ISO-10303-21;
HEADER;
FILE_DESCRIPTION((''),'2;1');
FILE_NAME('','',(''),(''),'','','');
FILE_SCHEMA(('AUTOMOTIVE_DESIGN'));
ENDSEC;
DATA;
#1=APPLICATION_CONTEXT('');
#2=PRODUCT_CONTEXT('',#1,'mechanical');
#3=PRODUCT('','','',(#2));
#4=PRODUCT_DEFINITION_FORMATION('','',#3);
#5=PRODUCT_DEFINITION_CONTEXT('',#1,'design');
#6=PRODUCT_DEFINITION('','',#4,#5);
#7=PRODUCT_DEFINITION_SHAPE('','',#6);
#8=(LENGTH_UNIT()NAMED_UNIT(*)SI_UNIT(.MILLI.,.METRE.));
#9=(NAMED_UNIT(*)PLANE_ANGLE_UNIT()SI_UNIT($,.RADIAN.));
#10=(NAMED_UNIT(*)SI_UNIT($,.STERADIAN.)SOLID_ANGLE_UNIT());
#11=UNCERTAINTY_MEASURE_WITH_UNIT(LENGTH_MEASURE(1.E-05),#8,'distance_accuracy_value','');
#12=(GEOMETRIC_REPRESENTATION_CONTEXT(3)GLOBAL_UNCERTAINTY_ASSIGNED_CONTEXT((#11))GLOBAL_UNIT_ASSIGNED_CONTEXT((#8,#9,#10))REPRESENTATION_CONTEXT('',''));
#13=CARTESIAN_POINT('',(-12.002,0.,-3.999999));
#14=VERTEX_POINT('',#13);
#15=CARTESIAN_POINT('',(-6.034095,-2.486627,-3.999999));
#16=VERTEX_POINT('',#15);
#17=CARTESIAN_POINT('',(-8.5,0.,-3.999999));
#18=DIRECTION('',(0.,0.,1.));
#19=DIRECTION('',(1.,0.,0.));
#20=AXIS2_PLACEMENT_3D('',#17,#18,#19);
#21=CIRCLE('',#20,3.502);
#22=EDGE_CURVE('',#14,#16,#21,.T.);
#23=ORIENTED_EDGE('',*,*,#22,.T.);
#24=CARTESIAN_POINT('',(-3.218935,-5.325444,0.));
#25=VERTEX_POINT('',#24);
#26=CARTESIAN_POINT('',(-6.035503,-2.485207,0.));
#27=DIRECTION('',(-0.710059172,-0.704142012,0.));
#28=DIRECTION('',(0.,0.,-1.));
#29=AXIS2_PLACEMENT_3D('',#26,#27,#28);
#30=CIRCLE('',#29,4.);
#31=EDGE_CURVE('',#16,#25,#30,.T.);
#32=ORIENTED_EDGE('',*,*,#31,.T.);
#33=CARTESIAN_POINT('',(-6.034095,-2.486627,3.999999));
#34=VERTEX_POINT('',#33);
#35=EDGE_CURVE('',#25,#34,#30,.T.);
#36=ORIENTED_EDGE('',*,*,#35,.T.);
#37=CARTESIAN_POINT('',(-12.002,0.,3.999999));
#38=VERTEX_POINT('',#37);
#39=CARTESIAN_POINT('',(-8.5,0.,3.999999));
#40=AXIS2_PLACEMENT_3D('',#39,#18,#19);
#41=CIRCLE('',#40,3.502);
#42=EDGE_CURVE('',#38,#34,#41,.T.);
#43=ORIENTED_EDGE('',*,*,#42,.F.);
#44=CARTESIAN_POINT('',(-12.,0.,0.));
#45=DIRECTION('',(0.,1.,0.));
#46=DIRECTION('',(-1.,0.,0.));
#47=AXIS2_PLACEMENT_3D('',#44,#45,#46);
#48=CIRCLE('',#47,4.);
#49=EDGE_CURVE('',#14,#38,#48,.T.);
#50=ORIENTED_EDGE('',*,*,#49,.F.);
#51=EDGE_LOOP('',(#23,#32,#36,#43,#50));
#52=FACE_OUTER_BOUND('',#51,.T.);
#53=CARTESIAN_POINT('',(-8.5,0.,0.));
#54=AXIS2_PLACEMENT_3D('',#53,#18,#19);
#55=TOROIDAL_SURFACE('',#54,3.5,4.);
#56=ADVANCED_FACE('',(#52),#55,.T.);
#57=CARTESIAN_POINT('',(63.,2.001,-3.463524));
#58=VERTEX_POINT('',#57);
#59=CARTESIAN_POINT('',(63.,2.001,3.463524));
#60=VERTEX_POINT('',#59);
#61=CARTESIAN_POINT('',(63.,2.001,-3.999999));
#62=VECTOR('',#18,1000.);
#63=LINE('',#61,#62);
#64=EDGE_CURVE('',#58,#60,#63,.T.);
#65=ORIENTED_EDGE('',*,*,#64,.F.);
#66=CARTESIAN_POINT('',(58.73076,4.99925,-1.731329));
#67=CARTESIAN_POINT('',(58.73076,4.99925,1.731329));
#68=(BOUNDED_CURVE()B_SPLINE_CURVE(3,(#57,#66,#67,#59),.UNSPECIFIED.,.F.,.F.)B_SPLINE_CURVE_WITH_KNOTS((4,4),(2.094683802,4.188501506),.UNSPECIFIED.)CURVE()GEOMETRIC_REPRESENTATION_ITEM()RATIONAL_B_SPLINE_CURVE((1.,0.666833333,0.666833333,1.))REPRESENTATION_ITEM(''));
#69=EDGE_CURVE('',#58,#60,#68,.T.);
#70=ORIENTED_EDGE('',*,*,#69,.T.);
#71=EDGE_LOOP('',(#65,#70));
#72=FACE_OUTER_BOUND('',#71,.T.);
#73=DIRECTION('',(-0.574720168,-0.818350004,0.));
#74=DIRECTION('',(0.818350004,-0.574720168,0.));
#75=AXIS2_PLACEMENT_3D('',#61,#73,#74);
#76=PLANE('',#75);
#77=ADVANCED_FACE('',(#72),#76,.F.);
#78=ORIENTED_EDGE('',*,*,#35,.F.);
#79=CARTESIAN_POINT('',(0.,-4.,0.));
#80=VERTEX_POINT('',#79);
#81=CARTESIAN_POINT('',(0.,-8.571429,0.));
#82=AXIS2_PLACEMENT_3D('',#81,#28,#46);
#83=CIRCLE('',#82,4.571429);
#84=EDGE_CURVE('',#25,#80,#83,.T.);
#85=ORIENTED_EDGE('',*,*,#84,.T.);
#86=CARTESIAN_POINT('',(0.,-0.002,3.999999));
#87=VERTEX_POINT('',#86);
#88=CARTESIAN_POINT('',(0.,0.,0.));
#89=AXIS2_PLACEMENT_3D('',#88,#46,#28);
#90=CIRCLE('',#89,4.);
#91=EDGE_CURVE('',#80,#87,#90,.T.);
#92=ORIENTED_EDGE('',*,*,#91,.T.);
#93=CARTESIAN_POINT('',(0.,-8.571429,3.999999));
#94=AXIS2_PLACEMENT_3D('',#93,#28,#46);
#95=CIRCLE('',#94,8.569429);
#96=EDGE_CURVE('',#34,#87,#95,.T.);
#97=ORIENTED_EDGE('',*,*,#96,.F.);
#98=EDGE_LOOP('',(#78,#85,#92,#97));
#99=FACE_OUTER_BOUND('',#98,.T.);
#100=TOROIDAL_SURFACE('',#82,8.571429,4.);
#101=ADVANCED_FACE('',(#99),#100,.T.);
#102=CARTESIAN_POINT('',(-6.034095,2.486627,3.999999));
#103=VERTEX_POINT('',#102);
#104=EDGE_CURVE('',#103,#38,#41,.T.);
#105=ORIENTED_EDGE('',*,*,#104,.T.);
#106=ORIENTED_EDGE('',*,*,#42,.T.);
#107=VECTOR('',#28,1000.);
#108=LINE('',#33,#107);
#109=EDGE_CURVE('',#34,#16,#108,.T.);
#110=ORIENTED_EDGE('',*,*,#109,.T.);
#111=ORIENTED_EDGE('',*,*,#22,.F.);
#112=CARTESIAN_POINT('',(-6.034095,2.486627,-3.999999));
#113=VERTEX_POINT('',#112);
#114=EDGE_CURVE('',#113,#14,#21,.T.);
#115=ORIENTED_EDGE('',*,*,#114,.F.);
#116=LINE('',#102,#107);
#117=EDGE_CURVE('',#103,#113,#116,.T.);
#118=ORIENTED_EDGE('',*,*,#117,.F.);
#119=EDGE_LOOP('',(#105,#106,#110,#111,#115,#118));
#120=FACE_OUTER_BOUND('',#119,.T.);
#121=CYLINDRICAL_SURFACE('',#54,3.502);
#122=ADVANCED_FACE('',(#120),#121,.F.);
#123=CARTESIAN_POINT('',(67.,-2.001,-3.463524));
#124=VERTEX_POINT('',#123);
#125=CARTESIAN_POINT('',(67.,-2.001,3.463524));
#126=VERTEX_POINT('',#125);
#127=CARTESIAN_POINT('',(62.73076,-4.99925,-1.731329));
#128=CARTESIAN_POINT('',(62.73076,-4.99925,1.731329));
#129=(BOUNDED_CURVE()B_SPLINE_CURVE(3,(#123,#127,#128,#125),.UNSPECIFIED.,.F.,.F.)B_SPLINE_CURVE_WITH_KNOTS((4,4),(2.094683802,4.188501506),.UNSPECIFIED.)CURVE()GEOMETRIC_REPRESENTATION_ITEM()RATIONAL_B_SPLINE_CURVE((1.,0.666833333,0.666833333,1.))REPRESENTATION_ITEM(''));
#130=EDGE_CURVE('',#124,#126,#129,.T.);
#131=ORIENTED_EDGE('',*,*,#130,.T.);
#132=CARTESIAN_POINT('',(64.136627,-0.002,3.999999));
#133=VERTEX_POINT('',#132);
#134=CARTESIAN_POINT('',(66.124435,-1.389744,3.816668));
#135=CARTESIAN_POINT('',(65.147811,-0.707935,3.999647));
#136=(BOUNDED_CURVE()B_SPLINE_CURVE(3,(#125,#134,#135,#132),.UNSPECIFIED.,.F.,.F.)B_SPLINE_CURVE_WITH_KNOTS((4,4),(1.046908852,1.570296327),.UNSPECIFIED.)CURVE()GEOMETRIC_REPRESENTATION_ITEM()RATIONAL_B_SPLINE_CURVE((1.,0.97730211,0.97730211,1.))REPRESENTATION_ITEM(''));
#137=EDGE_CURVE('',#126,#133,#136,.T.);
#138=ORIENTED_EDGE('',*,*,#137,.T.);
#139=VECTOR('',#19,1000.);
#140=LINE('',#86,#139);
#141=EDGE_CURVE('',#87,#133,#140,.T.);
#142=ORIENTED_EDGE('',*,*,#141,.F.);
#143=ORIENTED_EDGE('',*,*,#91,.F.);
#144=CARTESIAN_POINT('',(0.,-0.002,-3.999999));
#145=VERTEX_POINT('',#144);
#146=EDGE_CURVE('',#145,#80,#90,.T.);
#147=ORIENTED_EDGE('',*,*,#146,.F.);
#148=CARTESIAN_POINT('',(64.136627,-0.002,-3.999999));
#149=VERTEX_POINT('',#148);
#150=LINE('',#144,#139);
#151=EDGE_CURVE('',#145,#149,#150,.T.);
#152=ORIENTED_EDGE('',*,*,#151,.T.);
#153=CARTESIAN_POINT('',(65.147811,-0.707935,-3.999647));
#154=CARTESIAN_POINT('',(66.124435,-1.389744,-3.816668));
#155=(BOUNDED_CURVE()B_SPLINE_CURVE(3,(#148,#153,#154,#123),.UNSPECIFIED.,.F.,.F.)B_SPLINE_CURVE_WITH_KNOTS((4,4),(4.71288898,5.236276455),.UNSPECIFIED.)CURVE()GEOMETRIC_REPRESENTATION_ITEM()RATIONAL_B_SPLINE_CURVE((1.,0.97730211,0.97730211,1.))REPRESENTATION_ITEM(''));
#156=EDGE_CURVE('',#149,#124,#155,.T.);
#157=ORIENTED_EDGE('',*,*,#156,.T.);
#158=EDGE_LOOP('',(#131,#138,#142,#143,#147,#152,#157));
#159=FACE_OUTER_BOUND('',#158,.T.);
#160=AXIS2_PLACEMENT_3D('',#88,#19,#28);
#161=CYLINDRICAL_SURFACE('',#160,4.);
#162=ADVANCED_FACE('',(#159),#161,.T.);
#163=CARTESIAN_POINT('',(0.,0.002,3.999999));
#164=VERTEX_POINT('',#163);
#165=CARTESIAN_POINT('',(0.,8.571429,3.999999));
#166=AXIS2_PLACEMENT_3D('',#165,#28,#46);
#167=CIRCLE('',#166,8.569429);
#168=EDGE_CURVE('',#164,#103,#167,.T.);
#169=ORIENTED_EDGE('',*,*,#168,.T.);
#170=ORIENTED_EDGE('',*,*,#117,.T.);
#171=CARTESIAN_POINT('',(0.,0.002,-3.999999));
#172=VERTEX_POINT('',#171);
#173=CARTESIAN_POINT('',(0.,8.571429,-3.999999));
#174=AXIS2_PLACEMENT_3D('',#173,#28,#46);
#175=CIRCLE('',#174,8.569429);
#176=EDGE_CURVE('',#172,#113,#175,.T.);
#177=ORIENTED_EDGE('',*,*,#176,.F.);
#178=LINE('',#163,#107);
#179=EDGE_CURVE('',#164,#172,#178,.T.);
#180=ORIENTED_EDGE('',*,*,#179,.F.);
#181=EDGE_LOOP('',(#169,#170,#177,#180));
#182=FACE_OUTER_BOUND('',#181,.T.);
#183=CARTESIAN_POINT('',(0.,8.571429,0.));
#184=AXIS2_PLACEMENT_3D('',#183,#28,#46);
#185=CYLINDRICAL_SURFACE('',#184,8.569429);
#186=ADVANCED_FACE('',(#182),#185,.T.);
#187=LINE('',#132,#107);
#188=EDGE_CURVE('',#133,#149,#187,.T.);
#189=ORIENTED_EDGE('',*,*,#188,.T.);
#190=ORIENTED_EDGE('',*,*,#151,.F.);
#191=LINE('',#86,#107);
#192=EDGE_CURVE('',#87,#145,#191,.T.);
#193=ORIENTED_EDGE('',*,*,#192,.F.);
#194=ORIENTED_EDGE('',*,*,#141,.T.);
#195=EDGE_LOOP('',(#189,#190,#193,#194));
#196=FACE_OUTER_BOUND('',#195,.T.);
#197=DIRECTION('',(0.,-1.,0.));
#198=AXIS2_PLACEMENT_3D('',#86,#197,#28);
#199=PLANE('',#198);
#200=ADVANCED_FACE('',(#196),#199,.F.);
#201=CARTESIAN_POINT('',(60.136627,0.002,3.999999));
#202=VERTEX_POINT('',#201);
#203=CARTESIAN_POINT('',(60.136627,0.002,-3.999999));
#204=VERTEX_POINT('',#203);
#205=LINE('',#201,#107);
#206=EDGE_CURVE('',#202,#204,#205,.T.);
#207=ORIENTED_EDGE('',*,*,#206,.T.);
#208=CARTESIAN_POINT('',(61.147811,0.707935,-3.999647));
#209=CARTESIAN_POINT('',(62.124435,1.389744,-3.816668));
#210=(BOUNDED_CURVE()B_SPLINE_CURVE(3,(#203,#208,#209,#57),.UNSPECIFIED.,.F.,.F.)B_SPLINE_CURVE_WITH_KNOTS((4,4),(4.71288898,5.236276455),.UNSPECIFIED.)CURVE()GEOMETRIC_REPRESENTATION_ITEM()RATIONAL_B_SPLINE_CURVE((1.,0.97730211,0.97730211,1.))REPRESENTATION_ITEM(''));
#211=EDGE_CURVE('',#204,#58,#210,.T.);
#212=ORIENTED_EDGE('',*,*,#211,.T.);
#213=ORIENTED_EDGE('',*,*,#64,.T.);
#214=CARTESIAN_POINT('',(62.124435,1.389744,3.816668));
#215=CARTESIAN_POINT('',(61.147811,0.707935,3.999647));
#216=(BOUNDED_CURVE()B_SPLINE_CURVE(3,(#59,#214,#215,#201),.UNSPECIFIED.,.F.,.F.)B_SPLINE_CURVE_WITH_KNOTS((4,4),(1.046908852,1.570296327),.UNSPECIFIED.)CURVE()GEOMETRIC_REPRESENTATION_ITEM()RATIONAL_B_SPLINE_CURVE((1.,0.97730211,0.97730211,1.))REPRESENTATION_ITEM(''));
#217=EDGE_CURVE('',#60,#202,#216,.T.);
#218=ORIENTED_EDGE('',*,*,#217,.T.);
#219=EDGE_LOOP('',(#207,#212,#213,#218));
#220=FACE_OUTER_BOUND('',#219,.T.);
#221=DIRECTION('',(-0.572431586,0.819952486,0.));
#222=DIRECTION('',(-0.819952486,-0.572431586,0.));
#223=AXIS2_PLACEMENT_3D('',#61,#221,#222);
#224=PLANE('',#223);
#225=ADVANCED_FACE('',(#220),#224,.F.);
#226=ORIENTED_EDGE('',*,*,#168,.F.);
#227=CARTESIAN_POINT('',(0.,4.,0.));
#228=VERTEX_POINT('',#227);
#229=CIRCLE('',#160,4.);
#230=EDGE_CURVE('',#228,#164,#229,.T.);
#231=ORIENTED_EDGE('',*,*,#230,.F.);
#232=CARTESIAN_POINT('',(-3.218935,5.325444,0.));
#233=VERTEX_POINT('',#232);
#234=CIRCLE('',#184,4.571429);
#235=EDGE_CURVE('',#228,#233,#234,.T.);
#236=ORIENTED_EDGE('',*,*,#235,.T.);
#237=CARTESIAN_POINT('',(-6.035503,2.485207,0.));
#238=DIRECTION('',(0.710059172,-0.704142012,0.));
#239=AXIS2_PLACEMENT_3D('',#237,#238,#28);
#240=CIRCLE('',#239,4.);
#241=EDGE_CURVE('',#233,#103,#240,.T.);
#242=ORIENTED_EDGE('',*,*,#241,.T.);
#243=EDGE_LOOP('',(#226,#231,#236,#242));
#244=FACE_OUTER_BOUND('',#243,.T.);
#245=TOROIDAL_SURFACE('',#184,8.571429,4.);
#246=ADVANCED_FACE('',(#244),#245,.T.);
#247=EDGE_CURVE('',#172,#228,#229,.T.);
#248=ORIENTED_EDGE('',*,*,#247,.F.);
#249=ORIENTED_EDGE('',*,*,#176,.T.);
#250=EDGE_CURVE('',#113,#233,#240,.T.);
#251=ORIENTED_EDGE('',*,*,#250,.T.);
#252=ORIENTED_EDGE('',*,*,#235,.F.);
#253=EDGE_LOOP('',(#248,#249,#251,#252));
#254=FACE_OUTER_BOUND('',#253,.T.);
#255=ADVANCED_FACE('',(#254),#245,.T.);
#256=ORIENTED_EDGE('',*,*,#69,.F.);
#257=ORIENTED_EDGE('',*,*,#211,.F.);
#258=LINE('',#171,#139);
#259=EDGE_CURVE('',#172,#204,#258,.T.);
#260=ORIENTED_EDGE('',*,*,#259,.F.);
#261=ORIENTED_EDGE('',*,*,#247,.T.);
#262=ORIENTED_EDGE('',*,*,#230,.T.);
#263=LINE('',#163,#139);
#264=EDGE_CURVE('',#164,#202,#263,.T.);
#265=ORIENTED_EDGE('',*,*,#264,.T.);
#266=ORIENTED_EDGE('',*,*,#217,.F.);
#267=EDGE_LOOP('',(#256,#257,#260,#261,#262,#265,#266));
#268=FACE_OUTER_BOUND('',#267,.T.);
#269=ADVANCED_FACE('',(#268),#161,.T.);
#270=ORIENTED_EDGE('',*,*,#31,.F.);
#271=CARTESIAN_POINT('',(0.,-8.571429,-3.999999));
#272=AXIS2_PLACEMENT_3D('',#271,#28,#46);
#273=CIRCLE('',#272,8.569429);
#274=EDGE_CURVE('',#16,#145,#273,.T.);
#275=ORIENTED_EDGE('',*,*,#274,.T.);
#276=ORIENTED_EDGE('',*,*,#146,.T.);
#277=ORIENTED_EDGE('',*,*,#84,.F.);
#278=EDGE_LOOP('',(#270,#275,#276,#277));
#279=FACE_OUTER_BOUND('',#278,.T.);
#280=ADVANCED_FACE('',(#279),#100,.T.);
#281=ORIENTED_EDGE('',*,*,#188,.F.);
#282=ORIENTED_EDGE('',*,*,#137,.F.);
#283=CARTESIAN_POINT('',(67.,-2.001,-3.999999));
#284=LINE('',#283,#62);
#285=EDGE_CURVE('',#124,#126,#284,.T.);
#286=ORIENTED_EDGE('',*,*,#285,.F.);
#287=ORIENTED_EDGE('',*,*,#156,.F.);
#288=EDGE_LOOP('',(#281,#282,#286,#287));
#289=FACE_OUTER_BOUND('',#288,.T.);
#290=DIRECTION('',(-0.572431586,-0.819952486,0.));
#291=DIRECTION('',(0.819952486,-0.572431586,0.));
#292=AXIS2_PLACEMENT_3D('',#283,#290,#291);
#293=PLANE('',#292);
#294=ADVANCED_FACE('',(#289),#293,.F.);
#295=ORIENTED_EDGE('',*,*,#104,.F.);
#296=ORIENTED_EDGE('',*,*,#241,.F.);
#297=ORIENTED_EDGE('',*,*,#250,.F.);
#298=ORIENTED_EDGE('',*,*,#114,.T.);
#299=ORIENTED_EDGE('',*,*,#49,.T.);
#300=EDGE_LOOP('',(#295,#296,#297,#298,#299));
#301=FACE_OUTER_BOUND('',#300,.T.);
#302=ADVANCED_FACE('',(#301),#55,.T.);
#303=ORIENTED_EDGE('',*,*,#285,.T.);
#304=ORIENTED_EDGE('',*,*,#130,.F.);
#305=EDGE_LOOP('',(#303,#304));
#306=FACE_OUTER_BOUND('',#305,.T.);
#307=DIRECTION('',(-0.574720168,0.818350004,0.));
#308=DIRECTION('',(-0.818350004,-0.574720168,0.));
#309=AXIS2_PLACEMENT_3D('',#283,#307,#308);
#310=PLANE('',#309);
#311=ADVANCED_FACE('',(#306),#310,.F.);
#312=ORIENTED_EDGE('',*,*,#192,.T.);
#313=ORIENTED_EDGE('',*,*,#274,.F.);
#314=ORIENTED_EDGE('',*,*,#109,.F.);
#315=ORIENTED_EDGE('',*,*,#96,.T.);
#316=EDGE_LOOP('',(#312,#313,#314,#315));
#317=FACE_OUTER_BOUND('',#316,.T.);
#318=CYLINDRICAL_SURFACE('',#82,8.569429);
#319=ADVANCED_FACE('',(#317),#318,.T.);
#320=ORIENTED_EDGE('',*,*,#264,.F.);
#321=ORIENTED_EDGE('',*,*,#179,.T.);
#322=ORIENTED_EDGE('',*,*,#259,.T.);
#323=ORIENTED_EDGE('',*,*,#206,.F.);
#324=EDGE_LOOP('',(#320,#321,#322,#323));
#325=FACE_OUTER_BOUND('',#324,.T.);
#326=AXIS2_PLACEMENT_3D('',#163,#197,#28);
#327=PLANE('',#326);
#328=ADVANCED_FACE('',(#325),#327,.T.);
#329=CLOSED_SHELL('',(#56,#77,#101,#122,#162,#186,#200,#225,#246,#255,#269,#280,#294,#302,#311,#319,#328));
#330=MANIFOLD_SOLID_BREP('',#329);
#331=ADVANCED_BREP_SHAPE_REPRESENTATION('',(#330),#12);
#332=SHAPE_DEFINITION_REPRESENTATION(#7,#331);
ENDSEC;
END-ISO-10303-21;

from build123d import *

# Parameters (mm, degrees)
CONECUT_DEPTH      = 68.537026869
CONECUT_DEPTH_BACK = 68.537026869


with BuildPart() as part:
    # Body: sweep along a path in 草图2
    with BuildLine(Plane.XY) as body_path:
        Line((63, 4), (0, 4))
        ThreePointArc((0, 4), (-1.740570538, 4.344328693), (-3.218934911, 5.325443787))
        ThreePointArc((-3.218934911, 5.325443787), (-16, 0), (-3.218934911, -5.325443787))
        ThreePointArc((-3.218934911, -5.325443787), (-1.740570538, -4.344328693), (0, -4))
        Line((0, -4), (67, -4))
    # 草图1 → Body (sweep)
    with BuildSketch(Plane(origin=(63, 0, 0), x_dir=(0, 0, -1), z_dir=(1, 0, 0))):
        with BuildLine():
            Line((-3.9999995, 0.002), (3.9999995, 0.002))
            ThreePointArc((3.9999995, 0.002), (0, 4), (-3.9999995, 0.002))
        make_face()
    sweep(path=body_path.line)

    # 草图3 → ConeCut (cut, two sides: drawn at the far end of the back side and taken through both)
    with BuildSketch(Plane.XY.offset(-CONECUT_DEPTH_BACK)):
        Polygon((63, 2.001), (60.139364077, 4.01), (67.01, 4.01), (67.01, -4.01), (64.139364077, -4.01), (67, -2.001), (64.133762416, 0), (60.133762416, 0), align=None)
    extrude(amount=CONECUT_DEPTH + CONECUT_DEPTH_BACK, mode=Mode.SUBTRACT)


solid = part.part
